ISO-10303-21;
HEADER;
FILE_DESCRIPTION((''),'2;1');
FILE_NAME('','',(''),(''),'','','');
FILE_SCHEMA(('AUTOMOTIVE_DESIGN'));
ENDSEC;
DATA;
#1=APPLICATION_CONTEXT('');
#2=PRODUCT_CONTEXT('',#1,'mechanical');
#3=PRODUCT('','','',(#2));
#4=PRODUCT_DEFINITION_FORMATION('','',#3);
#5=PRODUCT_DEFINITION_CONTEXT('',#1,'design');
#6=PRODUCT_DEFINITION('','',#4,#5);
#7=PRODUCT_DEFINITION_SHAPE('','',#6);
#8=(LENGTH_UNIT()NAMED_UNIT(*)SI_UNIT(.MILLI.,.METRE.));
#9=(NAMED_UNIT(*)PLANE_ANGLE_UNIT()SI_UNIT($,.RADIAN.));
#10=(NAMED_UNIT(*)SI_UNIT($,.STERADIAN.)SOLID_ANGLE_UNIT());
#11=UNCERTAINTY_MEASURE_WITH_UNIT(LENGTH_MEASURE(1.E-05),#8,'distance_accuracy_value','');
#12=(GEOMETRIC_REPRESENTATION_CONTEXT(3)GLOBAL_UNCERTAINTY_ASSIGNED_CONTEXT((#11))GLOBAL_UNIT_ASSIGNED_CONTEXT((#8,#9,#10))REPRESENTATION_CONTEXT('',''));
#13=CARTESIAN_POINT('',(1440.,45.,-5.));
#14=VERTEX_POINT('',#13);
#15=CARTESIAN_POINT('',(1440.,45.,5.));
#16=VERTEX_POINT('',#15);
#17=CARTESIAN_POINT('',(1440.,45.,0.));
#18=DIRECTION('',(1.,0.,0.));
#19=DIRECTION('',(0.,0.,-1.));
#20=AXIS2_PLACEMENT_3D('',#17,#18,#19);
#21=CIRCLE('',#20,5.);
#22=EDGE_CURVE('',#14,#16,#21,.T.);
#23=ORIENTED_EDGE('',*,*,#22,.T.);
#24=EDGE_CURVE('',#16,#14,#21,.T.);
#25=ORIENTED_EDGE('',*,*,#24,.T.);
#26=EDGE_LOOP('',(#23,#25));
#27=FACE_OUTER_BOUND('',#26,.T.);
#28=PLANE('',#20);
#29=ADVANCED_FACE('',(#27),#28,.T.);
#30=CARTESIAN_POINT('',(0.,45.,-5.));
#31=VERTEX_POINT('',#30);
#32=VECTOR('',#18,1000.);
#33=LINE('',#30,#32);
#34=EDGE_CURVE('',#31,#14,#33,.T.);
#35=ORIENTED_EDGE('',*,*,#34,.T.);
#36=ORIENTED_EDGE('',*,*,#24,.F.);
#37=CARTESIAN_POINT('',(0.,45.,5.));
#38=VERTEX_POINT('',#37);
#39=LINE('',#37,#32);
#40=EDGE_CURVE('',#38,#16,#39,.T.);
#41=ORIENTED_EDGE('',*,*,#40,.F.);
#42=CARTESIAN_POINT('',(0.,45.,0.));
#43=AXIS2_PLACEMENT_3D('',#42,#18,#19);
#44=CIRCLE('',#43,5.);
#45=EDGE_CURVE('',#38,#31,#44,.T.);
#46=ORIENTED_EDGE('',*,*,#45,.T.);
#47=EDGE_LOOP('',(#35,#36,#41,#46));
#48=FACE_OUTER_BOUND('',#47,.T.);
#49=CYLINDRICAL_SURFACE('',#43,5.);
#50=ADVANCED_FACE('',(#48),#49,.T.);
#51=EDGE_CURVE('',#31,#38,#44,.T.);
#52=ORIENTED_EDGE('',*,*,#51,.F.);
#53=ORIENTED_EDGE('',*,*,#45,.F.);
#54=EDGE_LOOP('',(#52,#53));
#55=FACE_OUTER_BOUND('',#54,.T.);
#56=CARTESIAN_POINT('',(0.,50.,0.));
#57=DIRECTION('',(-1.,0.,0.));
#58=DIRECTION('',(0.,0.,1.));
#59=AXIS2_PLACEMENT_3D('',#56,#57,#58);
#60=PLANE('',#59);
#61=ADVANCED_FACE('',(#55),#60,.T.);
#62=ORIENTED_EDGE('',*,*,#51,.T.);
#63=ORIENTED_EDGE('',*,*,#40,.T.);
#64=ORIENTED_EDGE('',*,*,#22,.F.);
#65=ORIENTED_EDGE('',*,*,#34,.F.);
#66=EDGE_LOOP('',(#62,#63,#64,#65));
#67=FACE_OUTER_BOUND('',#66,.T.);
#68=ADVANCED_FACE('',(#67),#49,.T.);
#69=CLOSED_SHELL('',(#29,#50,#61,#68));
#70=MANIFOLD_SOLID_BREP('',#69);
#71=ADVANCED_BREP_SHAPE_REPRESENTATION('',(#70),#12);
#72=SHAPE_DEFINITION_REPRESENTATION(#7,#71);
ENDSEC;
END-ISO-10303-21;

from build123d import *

# Parameters (mm, degrees)
SKETCH_1_W = 1440
SKETCH_1_H = 5


with BuildPart() as part:
    # 草图1 → 旋转1 (revolve)
    with BuildSketch(Plane.XY, mode=Mode.PRIVATE) as revolve_1_sk:
        with Locations((720, 47.5)):
            Rectangle(SKETCH_1_W, SKETCH_1_H)
    revolve(revolve_1_sk.sketch.rotate(Axis((0, 45, 0), (1, 0, 0)), 270), axis=Axis((0, 45, 0), (1, 0, 0)))


solid = part.part
